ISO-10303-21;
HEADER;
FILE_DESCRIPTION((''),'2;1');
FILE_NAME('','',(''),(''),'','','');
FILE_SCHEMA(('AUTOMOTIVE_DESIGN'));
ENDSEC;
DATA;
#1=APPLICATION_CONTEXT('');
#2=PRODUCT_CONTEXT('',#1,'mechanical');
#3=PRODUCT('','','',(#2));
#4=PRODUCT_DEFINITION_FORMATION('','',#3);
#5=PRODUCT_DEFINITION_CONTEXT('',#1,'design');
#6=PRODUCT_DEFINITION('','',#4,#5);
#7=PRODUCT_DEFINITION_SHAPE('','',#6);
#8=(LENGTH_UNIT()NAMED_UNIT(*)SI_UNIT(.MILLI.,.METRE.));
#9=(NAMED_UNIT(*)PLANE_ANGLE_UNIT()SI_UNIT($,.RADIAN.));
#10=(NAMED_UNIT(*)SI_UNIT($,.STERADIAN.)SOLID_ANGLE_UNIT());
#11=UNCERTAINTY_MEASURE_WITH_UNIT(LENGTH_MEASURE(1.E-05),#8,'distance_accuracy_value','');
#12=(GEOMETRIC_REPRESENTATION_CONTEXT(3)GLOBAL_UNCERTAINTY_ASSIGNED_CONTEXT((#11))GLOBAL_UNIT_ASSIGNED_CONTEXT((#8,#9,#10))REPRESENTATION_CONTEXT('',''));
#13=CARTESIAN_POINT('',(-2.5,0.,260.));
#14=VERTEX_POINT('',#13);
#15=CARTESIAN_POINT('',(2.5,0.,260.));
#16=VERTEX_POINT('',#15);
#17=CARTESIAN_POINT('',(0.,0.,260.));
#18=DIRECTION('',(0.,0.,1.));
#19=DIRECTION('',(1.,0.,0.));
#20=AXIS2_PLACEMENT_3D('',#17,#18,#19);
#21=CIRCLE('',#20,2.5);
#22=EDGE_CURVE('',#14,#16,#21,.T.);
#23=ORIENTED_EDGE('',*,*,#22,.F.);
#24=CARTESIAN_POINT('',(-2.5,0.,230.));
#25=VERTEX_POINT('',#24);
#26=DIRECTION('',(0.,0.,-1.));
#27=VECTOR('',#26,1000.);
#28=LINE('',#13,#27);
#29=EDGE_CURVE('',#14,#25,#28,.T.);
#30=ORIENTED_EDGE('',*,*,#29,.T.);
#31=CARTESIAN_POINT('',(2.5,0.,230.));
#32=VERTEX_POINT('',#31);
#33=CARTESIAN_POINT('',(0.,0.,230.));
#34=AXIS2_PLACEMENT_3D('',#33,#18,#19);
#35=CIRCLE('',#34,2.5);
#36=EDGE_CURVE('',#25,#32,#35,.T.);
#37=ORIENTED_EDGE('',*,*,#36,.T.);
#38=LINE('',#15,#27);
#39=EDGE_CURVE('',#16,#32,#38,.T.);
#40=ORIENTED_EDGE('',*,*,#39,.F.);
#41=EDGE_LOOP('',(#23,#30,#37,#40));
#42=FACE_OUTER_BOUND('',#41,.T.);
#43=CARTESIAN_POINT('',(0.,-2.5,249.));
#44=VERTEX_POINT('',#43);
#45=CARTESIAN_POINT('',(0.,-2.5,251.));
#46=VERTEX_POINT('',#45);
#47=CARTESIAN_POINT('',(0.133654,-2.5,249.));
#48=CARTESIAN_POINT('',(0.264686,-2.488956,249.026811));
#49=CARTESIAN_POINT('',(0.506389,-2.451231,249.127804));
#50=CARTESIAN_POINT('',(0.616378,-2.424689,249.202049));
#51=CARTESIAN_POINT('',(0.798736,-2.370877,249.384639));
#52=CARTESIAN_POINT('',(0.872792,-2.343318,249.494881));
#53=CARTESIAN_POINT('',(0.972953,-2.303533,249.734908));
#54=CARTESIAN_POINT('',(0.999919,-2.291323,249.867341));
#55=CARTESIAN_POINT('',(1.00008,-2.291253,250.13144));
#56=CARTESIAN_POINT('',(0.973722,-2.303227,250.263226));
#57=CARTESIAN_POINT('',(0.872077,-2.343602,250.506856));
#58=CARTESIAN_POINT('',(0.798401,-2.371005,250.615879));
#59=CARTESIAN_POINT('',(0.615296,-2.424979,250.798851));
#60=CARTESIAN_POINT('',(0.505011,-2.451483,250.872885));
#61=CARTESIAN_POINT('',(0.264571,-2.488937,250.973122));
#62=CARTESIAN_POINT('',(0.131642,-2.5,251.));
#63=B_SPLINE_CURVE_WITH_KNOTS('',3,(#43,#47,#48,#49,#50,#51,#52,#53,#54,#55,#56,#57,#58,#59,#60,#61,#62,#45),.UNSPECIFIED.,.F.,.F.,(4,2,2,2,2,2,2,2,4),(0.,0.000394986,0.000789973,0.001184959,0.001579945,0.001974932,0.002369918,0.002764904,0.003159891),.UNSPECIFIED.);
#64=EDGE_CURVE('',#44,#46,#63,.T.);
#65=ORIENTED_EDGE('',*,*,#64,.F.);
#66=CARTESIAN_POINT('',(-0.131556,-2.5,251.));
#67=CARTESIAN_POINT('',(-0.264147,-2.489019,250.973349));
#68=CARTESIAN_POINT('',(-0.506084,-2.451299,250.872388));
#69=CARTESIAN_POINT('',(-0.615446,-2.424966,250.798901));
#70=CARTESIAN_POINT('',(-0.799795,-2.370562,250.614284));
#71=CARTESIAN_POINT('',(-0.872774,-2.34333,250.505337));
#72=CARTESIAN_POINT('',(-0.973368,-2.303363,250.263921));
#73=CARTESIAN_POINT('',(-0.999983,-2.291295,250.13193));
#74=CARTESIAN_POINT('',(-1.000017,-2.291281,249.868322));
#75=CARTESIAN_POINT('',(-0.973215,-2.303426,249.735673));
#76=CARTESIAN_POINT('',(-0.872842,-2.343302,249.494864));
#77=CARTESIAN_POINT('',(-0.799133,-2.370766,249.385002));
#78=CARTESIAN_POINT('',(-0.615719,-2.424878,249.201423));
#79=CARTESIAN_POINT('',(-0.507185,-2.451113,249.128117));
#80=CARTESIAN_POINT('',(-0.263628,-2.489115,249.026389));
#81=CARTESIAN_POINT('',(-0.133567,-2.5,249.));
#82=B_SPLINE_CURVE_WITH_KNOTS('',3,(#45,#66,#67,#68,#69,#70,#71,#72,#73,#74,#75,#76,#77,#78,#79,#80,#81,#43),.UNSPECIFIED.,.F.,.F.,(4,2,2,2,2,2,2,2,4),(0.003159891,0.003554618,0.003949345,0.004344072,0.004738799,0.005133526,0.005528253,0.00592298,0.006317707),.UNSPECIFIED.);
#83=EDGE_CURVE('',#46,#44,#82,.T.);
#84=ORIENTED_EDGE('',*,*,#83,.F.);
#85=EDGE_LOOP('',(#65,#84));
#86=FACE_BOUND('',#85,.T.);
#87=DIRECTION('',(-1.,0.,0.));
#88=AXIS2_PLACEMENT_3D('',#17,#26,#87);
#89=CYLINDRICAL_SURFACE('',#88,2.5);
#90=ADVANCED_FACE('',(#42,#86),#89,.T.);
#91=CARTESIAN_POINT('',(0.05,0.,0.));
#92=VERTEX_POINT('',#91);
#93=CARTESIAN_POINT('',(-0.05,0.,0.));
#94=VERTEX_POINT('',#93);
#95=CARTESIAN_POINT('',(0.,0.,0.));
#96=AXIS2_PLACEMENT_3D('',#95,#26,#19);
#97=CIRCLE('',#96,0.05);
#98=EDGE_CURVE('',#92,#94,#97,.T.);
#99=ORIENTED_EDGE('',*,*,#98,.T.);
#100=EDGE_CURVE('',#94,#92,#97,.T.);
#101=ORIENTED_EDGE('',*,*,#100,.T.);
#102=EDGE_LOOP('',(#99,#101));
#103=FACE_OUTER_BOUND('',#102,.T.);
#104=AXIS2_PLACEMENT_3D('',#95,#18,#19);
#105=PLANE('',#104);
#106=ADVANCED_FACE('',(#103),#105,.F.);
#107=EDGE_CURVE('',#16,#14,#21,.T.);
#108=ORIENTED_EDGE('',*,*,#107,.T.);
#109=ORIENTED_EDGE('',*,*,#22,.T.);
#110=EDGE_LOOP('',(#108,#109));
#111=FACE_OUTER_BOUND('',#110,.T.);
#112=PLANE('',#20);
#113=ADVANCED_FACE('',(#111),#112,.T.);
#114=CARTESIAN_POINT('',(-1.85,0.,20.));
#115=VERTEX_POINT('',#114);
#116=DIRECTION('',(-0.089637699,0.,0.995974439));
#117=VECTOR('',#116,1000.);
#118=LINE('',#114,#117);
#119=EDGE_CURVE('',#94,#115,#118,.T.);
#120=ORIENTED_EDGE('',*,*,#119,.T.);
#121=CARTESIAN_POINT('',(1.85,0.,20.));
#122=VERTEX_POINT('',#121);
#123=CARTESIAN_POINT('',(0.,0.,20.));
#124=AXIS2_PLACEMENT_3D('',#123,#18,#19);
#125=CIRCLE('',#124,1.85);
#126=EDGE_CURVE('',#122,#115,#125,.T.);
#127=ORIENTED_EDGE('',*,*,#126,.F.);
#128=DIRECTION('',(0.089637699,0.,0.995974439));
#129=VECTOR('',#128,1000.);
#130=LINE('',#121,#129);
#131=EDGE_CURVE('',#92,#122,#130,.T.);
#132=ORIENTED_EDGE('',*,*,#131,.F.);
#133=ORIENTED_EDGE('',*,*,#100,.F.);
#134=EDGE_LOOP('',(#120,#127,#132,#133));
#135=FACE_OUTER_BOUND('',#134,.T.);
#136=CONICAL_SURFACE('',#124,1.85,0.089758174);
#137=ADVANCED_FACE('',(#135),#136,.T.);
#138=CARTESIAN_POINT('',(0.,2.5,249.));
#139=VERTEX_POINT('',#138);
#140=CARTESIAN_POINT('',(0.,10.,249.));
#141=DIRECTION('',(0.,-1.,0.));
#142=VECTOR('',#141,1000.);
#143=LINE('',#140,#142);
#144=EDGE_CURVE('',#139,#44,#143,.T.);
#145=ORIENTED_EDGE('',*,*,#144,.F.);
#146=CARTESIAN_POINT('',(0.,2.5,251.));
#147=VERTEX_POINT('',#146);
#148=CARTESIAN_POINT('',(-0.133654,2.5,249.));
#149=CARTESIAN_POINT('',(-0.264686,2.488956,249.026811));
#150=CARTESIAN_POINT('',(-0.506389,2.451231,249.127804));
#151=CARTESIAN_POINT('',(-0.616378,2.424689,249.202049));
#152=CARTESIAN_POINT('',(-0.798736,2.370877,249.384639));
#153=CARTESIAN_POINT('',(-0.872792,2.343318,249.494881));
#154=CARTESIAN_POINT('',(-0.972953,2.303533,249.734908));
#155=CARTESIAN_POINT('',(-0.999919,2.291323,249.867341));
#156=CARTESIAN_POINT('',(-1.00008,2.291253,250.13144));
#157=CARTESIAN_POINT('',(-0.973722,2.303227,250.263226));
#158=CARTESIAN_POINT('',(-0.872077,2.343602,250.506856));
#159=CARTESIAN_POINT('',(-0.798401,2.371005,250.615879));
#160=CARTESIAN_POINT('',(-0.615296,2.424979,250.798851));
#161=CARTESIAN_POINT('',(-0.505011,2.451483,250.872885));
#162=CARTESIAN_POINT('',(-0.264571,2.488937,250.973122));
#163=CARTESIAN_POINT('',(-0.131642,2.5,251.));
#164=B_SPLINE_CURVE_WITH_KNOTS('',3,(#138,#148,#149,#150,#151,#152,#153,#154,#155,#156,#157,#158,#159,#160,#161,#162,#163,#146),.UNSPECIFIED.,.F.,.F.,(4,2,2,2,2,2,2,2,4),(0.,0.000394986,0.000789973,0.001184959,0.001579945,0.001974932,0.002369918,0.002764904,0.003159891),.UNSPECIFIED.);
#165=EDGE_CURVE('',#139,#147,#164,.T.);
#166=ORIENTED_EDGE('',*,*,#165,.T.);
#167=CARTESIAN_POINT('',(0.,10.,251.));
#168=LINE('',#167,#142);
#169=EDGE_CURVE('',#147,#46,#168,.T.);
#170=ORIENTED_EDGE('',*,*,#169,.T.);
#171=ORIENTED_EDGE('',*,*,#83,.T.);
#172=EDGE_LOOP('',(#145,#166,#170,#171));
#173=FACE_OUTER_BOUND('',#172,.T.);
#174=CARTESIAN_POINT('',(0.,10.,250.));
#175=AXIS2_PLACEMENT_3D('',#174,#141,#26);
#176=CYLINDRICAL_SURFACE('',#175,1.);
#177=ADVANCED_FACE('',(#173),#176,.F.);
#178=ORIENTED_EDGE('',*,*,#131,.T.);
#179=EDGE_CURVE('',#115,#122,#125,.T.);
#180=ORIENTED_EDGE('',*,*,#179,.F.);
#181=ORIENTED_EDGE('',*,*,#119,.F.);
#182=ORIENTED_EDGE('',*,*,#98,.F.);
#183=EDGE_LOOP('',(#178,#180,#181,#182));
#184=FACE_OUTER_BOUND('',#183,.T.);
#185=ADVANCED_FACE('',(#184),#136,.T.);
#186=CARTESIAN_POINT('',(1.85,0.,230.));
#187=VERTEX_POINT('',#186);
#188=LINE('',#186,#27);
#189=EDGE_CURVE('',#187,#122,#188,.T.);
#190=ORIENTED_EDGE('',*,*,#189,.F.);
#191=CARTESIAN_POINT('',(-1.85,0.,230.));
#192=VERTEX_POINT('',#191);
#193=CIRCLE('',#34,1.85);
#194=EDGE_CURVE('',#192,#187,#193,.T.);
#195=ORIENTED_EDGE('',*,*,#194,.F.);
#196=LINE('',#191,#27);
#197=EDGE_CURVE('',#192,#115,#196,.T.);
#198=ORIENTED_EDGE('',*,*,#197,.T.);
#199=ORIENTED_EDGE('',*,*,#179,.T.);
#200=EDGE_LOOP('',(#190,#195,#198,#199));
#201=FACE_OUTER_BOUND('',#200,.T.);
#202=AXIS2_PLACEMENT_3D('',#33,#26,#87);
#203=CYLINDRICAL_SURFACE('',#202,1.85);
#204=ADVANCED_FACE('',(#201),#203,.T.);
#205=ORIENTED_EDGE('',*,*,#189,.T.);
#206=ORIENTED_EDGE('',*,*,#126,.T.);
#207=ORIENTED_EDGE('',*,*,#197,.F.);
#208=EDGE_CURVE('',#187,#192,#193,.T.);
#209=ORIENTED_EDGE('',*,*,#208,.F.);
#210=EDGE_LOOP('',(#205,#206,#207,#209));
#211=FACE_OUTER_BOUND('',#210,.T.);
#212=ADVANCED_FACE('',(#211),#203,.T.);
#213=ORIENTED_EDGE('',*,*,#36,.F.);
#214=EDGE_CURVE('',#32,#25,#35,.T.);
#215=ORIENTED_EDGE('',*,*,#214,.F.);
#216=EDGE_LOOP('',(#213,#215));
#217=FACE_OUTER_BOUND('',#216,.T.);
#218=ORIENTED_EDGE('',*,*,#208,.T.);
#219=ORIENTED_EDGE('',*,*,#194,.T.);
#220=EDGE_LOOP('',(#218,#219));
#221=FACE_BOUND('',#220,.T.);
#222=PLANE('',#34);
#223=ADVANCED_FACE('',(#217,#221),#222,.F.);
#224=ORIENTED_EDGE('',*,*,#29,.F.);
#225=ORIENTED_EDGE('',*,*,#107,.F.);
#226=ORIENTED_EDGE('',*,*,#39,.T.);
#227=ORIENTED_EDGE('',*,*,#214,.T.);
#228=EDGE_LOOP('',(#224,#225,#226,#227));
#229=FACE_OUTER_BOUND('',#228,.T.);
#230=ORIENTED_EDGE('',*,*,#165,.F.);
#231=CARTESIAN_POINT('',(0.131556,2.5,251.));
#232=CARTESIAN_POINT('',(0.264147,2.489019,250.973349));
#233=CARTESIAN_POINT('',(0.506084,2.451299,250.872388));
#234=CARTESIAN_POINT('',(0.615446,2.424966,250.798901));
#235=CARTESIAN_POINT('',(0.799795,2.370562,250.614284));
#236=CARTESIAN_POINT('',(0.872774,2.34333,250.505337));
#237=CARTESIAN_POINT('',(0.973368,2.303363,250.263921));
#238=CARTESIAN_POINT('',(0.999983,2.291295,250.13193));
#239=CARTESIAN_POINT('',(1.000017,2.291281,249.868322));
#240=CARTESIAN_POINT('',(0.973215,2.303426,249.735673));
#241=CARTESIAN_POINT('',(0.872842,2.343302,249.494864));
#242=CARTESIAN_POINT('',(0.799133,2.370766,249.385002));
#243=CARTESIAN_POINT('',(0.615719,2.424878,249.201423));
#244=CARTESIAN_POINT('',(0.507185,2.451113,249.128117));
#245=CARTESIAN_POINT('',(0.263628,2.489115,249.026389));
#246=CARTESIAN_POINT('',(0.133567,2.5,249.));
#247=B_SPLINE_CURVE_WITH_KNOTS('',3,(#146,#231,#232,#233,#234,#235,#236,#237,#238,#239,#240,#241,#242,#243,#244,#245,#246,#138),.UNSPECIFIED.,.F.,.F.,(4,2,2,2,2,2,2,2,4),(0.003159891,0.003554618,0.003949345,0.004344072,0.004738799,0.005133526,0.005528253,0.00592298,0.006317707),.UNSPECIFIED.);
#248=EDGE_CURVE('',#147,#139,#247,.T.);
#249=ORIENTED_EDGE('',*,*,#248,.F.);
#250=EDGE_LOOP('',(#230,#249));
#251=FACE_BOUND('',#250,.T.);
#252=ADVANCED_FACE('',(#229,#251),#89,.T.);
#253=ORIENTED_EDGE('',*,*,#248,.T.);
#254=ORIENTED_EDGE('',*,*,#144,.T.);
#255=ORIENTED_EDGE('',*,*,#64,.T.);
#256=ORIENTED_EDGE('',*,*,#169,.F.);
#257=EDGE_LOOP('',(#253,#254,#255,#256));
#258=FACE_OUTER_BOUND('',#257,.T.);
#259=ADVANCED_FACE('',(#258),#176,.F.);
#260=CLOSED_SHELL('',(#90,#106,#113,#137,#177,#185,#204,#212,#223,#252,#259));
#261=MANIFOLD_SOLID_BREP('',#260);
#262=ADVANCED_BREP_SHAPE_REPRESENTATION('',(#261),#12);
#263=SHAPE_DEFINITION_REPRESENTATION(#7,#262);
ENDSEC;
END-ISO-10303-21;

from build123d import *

# Parameters (mm, degrees)
SKETCH1_R               = 1.85
BOSS_EXTRUDE1_DEPTH     = 230
SKETCH2_R               = 2.5
BOSS_EXTRUDE2_DEPTH     = 30
CHAMFER1_SIZE           = 1.8
CHAMFER1_SIZE2          = 20
CUT_EXTRUDE1_DEPTH      = 10
CUT_EXTRUDE1_DEPTH_BACK = 10
SKETCH_3_2_R            = 1


with BuildPart() as part:
    # Sketch1 → Boss-Extrude1 (new body)
    with BuildSketch(Plane.XY):
        Circle(SKETCH1_R)
    extrude(amount=BOSS_EXTRUDE1_DEPTH)

    # Sketch2 → Boss-Extrude2 (add)
    with BuildSketch(Plane.XY.offset(230)):
        Circle(SKETCH2_R)
    extrude(amount=BOSS_EXTRUDE2_DEPTH)

    # Chamfer1
    chamfer1_edges = [part.edges().sort_by_distance(p)[0] for p in [
        (-1.85, 0, 0),
    ]]
    chamfer1_side = [part.faces().sort_by_distance(p)[0] for p in [
        (0, 0, 0),
    ]]
    chamfer(chamfer1_edges, length=CHAMFER1_SIZE, length2=CHAMFER1_SIZE2, reference=chamfer1_side[0])

    # Sketch 3_2 → Cut-Extrude1 (cut, two sides: drawn at the far end of the back side and taken through both)
    with BuildSketch(Plane(origin=(0, 0, 0), x_dir=(1, 0, 0), z_dir=(0, 1, 0)).offset(-CUT_EXTRUDE1_DEPTH_BACK)):
        with Locations(Location((0, -250, 0), (0, 0, 90))):
            Circle(SKETCH_3_2_R)
    extrude(amount=CUT_EXTRUDE1_DEPTH + CUT_EXTRUDE1_DEPTH_BACK, mode=Mode.SUBTRACT)


solid = part.part
